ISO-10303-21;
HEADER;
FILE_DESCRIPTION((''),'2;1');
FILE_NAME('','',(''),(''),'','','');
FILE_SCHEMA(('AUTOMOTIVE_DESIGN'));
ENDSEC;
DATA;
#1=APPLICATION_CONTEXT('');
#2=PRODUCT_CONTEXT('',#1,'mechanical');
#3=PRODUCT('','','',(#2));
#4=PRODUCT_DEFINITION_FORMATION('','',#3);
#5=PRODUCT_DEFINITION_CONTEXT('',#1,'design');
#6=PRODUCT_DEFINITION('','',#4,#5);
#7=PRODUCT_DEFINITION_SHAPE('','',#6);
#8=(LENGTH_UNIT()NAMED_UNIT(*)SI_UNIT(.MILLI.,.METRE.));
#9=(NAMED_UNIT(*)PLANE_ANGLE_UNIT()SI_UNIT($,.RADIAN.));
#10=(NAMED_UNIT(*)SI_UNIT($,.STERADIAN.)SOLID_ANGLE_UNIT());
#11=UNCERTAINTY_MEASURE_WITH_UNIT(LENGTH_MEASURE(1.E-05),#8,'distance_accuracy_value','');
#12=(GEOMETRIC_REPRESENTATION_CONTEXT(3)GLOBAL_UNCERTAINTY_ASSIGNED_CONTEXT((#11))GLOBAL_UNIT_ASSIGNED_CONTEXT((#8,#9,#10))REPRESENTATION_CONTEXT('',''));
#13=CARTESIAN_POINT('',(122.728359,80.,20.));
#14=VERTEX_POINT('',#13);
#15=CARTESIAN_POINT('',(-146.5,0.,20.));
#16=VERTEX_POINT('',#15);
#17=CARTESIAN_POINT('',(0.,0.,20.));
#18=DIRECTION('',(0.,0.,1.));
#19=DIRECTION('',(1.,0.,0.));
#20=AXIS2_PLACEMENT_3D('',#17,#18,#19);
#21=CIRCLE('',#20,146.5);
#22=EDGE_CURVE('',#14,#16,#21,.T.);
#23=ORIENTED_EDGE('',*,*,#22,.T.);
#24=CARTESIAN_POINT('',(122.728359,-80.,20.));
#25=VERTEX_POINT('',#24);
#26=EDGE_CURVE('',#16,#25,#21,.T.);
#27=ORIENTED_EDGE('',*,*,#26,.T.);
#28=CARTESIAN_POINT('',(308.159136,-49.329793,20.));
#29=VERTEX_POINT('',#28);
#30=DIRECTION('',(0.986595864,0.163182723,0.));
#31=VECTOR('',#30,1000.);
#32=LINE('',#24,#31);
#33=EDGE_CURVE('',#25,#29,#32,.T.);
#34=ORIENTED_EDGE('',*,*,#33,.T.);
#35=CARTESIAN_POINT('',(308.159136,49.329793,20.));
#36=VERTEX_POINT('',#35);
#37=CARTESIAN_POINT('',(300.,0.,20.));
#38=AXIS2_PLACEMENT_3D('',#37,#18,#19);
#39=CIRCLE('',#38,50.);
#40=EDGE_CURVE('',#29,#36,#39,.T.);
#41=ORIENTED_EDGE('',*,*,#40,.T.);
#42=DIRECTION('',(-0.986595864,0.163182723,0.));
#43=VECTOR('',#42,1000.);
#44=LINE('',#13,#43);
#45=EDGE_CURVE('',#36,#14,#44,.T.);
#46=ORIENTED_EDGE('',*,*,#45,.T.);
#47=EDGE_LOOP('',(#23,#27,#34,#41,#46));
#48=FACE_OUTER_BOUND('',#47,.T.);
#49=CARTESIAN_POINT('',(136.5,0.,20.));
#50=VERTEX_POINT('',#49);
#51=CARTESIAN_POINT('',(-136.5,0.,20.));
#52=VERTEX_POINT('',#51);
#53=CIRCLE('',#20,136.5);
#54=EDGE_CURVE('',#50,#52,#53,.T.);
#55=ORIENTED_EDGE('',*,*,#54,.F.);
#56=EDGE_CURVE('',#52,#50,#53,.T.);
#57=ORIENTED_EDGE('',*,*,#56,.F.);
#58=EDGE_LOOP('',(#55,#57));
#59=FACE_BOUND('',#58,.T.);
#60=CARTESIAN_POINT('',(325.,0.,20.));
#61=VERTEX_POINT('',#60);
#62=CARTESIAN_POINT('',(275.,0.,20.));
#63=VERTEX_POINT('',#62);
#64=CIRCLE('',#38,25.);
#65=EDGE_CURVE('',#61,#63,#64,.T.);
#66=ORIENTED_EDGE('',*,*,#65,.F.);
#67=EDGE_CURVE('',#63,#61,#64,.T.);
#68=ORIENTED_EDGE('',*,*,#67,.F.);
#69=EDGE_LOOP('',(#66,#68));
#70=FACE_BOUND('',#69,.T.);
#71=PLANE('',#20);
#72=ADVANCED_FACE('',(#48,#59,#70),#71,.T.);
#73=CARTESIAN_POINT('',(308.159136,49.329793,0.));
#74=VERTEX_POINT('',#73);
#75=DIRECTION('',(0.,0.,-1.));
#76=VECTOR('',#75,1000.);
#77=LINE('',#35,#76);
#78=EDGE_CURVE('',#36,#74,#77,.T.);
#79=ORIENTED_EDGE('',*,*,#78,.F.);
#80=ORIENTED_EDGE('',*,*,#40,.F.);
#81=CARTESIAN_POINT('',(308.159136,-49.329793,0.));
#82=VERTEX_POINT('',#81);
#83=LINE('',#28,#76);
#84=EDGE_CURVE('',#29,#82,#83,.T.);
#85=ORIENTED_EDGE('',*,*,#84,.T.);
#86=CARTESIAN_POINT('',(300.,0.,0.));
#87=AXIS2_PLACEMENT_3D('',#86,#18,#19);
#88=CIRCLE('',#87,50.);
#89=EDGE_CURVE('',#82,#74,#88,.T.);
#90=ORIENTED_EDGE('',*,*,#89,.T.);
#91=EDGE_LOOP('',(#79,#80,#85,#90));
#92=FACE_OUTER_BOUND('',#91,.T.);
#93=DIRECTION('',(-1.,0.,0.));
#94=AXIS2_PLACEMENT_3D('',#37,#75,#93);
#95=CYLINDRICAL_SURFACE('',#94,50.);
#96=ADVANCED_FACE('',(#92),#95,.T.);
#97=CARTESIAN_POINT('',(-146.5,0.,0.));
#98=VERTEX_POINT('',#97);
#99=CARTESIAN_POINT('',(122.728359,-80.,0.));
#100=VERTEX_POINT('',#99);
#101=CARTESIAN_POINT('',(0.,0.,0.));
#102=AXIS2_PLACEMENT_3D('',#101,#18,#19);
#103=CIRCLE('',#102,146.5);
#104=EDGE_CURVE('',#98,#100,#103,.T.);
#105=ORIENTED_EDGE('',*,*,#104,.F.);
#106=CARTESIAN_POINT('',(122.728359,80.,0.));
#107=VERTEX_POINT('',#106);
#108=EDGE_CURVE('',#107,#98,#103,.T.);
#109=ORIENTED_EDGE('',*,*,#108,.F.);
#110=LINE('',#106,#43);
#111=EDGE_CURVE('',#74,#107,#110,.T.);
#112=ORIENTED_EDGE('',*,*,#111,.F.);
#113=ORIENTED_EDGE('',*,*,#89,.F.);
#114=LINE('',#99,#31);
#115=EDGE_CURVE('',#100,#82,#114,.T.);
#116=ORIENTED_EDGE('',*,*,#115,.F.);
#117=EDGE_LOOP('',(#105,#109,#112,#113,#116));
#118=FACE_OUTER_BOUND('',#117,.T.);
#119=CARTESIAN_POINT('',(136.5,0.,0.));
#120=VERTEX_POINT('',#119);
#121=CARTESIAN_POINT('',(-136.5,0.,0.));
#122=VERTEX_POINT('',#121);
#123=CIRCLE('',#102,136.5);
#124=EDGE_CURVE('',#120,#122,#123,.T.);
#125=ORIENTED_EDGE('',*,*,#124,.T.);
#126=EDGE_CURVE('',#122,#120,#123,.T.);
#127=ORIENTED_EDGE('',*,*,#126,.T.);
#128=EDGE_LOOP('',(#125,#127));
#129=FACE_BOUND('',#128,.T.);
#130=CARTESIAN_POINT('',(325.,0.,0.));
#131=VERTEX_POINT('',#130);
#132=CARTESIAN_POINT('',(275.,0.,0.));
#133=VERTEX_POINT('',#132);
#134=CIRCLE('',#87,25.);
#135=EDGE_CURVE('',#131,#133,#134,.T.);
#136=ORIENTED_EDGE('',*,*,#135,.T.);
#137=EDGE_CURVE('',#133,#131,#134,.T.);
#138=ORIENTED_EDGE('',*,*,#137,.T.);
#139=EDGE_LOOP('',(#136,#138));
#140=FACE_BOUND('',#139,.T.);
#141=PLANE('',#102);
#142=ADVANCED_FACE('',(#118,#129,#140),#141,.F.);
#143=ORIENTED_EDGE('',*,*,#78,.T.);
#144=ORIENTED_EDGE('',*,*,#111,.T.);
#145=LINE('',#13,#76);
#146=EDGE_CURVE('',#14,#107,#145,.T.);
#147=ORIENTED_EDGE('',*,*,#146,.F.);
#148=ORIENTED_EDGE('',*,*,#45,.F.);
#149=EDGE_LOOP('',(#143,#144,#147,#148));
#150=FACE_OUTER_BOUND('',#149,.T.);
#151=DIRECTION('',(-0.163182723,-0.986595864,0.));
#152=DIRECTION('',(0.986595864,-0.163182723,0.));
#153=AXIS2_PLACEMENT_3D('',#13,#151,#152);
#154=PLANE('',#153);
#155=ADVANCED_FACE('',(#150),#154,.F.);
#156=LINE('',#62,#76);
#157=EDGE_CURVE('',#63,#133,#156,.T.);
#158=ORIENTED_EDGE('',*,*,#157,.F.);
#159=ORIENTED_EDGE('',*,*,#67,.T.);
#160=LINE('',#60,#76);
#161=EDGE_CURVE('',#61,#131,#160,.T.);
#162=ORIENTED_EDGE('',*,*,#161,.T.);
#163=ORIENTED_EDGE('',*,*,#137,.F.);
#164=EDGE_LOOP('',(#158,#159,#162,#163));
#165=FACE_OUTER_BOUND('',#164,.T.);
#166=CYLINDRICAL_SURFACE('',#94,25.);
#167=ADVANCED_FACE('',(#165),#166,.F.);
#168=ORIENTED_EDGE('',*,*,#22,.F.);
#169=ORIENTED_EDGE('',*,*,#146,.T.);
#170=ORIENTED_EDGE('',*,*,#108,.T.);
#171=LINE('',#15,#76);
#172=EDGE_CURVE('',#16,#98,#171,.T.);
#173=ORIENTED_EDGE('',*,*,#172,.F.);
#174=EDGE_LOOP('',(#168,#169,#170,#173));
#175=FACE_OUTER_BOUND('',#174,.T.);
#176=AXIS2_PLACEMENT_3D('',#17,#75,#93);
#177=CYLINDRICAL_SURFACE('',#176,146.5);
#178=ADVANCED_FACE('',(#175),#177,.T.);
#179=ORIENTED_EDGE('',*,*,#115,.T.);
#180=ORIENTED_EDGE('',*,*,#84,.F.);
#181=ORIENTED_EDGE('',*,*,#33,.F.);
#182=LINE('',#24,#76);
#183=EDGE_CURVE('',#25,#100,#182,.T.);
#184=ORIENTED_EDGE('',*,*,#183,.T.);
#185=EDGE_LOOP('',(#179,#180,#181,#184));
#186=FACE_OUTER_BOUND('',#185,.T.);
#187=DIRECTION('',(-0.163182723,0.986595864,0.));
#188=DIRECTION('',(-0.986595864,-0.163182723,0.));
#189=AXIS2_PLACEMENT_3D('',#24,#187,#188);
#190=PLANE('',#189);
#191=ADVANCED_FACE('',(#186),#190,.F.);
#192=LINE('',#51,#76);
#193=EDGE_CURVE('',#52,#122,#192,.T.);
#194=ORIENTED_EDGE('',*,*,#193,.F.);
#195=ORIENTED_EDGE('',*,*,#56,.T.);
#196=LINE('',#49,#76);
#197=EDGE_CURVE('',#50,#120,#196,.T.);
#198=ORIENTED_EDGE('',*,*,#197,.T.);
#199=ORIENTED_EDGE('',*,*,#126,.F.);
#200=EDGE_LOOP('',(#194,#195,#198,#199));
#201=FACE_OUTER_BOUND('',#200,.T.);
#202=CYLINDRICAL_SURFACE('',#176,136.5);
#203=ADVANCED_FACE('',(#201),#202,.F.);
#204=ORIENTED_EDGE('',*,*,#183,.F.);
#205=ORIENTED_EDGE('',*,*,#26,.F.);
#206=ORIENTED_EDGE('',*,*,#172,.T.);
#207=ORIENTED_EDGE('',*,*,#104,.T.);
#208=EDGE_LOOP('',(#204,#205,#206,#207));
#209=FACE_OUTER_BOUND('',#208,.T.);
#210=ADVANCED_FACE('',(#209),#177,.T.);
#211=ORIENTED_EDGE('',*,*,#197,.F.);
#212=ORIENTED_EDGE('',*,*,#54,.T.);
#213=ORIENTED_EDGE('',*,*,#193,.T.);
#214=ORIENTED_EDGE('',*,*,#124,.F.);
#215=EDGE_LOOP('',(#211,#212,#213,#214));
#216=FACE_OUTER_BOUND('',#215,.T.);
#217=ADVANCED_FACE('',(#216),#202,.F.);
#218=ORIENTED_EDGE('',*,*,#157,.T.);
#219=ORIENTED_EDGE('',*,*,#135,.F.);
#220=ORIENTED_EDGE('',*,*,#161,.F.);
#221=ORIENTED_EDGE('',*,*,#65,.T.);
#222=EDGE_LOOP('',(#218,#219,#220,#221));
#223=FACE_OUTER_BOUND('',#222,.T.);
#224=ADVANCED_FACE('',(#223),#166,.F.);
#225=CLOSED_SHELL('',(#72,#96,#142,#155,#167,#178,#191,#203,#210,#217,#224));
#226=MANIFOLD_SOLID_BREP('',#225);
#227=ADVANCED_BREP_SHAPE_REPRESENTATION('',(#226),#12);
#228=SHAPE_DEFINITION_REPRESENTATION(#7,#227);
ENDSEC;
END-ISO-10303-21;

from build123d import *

# Parameters (mm, degrees)
SKETCH1_R           = 25
SKETCH1_R_2         = 136.5
BOSS_EXTRUDE1_DEPTH = 20


with BuildPart() as part:
    # Sketch1 → Boss-Extrude1 (new body)
    with BuildSketch(Plane.XY):
        with BuildLine():
            Line((122.728358581, 80), (308.159136141, 49.329793203))
            ThreePointArc((308.159136141, 49.329793203), (350, 0), (308.159136141, -49.329793203))
            Line((308.159136141, -49.329793203), (122.728358581, -80))
            ThreePointArc((122.728358581, -80), (-146.5, 0), (122.728358581, 80))
        make_face()
        with Locations((300, 0)):
            Circle(SKETCH1_R, mode=Mode.SUBTRACT)
        Circle(SKETCH1_R_2, mode=Mode.SUBTRACT)
    extrude(amount=BOSS_EXTRUDE1_DEPTH)


solid = part.part
